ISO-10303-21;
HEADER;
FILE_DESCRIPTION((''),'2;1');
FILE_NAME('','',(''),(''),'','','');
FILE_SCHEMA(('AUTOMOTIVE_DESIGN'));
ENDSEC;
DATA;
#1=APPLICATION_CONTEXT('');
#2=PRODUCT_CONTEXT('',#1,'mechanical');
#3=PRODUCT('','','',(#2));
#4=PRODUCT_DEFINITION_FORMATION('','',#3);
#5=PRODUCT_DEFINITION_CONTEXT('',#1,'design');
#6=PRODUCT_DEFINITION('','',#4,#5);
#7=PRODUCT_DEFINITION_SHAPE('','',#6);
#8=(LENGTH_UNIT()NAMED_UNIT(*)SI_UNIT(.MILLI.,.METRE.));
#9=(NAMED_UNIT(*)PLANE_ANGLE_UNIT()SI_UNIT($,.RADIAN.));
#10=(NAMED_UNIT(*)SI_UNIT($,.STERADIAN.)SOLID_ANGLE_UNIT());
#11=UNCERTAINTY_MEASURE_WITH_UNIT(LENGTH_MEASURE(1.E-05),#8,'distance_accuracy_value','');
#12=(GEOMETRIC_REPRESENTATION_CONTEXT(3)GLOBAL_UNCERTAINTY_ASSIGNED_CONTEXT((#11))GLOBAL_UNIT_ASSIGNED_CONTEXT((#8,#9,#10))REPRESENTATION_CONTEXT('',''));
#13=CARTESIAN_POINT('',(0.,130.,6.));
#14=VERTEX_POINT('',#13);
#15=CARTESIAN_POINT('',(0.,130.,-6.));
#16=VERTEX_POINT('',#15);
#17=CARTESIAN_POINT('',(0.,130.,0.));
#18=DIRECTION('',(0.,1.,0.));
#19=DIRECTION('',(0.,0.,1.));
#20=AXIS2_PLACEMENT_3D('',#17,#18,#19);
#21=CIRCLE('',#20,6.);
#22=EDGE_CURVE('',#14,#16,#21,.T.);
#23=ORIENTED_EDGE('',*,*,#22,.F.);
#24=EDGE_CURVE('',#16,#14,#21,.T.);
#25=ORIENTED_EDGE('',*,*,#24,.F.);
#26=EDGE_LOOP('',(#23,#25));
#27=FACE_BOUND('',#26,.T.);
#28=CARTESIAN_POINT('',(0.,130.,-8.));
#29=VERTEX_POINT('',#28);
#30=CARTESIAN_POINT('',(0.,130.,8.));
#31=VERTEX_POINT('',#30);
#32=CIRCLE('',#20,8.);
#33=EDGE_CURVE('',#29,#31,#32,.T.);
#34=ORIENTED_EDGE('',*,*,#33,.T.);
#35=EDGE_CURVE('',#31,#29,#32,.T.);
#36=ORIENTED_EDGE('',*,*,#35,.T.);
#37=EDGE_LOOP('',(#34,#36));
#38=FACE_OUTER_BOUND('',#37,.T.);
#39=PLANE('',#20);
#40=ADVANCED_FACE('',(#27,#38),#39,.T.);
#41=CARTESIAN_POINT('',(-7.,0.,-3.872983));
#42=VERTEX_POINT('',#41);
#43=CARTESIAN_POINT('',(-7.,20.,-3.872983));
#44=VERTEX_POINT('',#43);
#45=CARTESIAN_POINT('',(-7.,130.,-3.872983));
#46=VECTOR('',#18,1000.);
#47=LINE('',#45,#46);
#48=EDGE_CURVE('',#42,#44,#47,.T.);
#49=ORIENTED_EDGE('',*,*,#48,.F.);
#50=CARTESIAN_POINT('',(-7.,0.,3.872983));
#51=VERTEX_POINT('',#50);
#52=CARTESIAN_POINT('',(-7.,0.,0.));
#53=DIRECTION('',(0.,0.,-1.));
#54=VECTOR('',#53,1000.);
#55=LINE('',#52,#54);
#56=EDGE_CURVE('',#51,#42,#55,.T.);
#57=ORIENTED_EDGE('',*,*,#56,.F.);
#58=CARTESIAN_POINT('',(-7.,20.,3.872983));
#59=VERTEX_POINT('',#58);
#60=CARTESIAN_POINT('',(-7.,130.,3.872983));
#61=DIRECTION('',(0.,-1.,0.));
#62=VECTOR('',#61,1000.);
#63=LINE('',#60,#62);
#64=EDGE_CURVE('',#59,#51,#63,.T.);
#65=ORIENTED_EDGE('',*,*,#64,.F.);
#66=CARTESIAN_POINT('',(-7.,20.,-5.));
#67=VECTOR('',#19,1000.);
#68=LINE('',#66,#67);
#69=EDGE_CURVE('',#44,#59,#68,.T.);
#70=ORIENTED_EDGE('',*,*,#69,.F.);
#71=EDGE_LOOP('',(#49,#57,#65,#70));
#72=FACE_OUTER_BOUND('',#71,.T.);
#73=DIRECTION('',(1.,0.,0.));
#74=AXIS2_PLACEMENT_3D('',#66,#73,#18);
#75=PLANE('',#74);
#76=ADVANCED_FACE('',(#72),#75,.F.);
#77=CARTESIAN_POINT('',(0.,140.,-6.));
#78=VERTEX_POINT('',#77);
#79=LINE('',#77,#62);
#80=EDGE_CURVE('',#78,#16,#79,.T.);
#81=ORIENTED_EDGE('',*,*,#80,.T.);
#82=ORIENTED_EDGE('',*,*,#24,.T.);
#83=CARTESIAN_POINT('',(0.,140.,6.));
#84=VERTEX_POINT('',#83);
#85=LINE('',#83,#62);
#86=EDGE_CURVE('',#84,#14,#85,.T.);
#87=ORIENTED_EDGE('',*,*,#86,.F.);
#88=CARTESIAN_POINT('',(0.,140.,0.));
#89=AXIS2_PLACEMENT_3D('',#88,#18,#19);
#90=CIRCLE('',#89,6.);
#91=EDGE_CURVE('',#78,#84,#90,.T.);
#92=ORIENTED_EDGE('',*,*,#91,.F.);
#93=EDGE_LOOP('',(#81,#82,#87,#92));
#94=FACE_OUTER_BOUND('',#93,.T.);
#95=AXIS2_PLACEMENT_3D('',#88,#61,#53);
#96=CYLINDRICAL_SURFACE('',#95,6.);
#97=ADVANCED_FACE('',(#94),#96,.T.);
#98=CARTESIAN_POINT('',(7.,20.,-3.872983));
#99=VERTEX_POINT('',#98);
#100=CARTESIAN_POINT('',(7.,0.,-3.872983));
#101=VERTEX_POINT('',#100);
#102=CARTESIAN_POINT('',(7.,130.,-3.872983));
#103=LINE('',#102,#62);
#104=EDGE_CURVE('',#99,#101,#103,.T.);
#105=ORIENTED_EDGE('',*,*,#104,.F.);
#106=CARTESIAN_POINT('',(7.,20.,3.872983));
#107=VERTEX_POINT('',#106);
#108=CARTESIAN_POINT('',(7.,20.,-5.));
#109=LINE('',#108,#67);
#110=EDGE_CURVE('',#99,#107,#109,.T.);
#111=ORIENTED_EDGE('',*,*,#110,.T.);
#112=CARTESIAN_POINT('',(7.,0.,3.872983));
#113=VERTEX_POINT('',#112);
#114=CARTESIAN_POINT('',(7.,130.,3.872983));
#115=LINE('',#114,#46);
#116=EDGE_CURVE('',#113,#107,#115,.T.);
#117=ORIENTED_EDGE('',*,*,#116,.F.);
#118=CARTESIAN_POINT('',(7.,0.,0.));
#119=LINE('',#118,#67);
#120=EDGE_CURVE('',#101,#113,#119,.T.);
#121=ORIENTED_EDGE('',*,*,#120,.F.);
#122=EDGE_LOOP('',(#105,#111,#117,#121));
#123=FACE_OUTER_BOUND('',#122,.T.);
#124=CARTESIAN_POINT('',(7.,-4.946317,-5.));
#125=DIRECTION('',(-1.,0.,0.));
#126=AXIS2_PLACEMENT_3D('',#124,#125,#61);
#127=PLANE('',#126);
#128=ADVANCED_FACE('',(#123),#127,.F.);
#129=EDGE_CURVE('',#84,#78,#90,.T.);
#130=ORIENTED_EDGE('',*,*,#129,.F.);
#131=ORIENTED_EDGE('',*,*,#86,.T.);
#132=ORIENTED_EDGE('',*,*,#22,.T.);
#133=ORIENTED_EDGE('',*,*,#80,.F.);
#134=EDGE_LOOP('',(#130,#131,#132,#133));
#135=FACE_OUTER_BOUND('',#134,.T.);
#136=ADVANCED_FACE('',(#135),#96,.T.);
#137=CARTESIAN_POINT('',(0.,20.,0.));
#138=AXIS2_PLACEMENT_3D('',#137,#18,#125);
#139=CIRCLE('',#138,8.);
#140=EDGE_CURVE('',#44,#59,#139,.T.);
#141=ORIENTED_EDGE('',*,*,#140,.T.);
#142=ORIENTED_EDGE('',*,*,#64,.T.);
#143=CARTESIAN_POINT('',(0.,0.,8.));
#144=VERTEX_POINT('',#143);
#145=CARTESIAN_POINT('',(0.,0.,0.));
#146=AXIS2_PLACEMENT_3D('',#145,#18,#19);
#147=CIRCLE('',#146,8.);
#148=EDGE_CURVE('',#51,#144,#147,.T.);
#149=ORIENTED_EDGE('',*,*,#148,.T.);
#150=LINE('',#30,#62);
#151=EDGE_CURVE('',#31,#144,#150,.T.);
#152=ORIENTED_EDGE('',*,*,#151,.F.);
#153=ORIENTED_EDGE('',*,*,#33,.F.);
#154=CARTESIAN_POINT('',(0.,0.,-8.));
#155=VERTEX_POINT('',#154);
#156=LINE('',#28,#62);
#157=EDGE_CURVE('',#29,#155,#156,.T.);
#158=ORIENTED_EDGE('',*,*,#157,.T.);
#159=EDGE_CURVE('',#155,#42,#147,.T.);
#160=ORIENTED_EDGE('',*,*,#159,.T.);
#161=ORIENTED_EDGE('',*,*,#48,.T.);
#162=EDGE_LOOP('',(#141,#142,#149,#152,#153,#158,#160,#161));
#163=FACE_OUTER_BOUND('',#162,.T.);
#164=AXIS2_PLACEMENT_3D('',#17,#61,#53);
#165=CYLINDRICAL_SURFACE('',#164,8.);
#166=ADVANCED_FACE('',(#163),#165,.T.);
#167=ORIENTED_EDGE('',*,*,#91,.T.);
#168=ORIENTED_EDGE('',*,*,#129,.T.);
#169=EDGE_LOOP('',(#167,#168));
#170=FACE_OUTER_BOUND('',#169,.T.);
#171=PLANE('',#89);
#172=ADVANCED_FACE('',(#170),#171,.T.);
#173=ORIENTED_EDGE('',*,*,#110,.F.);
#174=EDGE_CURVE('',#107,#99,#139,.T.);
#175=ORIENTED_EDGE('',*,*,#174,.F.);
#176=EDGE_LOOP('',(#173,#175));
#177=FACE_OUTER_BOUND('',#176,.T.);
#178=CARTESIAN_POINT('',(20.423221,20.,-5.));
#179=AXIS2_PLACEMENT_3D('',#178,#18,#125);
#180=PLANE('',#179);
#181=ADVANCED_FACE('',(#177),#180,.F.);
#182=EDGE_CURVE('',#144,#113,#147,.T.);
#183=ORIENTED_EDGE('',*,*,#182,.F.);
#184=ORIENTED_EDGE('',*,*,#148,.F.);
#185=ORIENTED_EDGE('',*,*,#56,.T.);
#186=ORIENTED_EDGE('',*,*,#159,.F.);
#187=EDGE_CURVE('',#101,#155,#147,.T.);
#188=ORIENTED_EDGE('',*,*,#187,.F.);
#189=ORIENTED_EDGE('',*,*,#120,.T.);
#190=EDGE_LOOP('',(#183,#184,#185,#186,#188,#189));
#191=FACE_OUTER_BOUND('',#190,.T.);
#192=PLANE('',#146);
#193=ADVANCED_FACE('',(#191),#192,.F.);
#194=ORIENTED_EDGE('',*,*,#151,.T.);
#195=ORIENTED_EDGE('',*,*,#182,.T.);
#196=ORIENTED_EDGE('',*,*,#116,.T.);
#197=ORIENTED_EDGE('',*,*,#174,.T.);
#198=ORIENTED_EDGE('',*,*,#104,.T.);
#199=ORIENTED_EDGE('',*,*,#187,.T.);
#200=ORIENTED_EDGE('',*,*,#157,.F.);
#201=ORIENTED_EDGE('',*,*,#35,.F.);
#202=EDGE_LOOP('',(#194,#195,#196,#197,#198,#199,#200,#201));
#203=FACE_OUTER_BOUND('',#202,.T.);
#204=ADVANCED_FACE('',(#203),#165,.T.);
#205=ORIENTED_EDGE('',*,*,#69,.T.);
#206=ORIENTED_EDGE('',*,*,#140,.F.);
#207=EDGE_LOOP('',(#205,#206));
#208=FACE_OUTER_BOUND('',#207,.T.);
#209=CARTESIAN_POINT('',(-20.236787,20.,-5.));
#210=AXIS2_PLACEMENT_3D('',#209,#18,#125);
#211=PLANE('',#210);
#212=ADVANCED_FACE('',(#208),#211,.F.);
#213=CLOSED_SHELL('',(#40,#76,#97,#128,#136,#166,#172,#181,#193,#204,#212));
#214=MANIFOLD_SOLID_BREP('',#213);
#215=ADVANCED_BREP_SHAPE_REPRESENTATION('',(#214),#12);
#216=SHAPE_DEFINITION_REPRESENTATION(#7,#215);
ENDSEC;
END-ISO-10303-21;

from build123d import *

# Parameters (mm, degrees)
SKETCH1_R           = 8
BOSS_EXTRUDE1_DEPTH = 130
SKETCH4_R           = 6
BOSS_EXTRUDE2_DEPTH = 10
SKETCH5_W           = 13.236787349
SKETCH5_H           = 35.235955056
SKETCH5_W_2         = 13.423220974
SKETCH5_H_2         = 24.946317104
CUT_EXTRUDE1_DEPTH  = 5


with BuildPart() as part:
    # Sketch1 → Boss-Extrude1 (new body)
    with BuildSketch(Plane(origin=(0, 0, 0), x_dir=(1, 0, 0), z_dir=(0, 1, 0))):
        with Locations(Location((0, 0, 0), (0, 0, 270))):
            Circle(SKETCH1_R)
    extrude(amount=BOSS_EXTRUDE1_DEPTH)

    # Sketch4 → Boss-Extrude2 (add)
    with BuildSketch(Plane(origin=(0, 130, 0), x_dir=(1, 0, 0), z_dir=(0, 1, 0))):
        with Locations(Location((0, 0, 0), (0, 0, 270))):
            Circle(SKETCH4_R)
    extrude(amount=BOSS_EXTRUDE2_DEPTH)

    # Sketch5 → Cut-Extrude1 (cut, symmetric)
    with BuildSketch(Plane.XY):
        with Locations((-13.618393675, 2.382022472)):
            Rectangle(SKETCH5_W, SKETCH5_H)
        with Locations((13.711610487, 7.526841448)):
            Rectangle(SKETCH5_W_2, SKETCH5_H_2)
    extrude(amount=CUT_EXTRUDE1_DEPTH, both=True, mode=Mode.SUBTRACT)


solid = part.part
